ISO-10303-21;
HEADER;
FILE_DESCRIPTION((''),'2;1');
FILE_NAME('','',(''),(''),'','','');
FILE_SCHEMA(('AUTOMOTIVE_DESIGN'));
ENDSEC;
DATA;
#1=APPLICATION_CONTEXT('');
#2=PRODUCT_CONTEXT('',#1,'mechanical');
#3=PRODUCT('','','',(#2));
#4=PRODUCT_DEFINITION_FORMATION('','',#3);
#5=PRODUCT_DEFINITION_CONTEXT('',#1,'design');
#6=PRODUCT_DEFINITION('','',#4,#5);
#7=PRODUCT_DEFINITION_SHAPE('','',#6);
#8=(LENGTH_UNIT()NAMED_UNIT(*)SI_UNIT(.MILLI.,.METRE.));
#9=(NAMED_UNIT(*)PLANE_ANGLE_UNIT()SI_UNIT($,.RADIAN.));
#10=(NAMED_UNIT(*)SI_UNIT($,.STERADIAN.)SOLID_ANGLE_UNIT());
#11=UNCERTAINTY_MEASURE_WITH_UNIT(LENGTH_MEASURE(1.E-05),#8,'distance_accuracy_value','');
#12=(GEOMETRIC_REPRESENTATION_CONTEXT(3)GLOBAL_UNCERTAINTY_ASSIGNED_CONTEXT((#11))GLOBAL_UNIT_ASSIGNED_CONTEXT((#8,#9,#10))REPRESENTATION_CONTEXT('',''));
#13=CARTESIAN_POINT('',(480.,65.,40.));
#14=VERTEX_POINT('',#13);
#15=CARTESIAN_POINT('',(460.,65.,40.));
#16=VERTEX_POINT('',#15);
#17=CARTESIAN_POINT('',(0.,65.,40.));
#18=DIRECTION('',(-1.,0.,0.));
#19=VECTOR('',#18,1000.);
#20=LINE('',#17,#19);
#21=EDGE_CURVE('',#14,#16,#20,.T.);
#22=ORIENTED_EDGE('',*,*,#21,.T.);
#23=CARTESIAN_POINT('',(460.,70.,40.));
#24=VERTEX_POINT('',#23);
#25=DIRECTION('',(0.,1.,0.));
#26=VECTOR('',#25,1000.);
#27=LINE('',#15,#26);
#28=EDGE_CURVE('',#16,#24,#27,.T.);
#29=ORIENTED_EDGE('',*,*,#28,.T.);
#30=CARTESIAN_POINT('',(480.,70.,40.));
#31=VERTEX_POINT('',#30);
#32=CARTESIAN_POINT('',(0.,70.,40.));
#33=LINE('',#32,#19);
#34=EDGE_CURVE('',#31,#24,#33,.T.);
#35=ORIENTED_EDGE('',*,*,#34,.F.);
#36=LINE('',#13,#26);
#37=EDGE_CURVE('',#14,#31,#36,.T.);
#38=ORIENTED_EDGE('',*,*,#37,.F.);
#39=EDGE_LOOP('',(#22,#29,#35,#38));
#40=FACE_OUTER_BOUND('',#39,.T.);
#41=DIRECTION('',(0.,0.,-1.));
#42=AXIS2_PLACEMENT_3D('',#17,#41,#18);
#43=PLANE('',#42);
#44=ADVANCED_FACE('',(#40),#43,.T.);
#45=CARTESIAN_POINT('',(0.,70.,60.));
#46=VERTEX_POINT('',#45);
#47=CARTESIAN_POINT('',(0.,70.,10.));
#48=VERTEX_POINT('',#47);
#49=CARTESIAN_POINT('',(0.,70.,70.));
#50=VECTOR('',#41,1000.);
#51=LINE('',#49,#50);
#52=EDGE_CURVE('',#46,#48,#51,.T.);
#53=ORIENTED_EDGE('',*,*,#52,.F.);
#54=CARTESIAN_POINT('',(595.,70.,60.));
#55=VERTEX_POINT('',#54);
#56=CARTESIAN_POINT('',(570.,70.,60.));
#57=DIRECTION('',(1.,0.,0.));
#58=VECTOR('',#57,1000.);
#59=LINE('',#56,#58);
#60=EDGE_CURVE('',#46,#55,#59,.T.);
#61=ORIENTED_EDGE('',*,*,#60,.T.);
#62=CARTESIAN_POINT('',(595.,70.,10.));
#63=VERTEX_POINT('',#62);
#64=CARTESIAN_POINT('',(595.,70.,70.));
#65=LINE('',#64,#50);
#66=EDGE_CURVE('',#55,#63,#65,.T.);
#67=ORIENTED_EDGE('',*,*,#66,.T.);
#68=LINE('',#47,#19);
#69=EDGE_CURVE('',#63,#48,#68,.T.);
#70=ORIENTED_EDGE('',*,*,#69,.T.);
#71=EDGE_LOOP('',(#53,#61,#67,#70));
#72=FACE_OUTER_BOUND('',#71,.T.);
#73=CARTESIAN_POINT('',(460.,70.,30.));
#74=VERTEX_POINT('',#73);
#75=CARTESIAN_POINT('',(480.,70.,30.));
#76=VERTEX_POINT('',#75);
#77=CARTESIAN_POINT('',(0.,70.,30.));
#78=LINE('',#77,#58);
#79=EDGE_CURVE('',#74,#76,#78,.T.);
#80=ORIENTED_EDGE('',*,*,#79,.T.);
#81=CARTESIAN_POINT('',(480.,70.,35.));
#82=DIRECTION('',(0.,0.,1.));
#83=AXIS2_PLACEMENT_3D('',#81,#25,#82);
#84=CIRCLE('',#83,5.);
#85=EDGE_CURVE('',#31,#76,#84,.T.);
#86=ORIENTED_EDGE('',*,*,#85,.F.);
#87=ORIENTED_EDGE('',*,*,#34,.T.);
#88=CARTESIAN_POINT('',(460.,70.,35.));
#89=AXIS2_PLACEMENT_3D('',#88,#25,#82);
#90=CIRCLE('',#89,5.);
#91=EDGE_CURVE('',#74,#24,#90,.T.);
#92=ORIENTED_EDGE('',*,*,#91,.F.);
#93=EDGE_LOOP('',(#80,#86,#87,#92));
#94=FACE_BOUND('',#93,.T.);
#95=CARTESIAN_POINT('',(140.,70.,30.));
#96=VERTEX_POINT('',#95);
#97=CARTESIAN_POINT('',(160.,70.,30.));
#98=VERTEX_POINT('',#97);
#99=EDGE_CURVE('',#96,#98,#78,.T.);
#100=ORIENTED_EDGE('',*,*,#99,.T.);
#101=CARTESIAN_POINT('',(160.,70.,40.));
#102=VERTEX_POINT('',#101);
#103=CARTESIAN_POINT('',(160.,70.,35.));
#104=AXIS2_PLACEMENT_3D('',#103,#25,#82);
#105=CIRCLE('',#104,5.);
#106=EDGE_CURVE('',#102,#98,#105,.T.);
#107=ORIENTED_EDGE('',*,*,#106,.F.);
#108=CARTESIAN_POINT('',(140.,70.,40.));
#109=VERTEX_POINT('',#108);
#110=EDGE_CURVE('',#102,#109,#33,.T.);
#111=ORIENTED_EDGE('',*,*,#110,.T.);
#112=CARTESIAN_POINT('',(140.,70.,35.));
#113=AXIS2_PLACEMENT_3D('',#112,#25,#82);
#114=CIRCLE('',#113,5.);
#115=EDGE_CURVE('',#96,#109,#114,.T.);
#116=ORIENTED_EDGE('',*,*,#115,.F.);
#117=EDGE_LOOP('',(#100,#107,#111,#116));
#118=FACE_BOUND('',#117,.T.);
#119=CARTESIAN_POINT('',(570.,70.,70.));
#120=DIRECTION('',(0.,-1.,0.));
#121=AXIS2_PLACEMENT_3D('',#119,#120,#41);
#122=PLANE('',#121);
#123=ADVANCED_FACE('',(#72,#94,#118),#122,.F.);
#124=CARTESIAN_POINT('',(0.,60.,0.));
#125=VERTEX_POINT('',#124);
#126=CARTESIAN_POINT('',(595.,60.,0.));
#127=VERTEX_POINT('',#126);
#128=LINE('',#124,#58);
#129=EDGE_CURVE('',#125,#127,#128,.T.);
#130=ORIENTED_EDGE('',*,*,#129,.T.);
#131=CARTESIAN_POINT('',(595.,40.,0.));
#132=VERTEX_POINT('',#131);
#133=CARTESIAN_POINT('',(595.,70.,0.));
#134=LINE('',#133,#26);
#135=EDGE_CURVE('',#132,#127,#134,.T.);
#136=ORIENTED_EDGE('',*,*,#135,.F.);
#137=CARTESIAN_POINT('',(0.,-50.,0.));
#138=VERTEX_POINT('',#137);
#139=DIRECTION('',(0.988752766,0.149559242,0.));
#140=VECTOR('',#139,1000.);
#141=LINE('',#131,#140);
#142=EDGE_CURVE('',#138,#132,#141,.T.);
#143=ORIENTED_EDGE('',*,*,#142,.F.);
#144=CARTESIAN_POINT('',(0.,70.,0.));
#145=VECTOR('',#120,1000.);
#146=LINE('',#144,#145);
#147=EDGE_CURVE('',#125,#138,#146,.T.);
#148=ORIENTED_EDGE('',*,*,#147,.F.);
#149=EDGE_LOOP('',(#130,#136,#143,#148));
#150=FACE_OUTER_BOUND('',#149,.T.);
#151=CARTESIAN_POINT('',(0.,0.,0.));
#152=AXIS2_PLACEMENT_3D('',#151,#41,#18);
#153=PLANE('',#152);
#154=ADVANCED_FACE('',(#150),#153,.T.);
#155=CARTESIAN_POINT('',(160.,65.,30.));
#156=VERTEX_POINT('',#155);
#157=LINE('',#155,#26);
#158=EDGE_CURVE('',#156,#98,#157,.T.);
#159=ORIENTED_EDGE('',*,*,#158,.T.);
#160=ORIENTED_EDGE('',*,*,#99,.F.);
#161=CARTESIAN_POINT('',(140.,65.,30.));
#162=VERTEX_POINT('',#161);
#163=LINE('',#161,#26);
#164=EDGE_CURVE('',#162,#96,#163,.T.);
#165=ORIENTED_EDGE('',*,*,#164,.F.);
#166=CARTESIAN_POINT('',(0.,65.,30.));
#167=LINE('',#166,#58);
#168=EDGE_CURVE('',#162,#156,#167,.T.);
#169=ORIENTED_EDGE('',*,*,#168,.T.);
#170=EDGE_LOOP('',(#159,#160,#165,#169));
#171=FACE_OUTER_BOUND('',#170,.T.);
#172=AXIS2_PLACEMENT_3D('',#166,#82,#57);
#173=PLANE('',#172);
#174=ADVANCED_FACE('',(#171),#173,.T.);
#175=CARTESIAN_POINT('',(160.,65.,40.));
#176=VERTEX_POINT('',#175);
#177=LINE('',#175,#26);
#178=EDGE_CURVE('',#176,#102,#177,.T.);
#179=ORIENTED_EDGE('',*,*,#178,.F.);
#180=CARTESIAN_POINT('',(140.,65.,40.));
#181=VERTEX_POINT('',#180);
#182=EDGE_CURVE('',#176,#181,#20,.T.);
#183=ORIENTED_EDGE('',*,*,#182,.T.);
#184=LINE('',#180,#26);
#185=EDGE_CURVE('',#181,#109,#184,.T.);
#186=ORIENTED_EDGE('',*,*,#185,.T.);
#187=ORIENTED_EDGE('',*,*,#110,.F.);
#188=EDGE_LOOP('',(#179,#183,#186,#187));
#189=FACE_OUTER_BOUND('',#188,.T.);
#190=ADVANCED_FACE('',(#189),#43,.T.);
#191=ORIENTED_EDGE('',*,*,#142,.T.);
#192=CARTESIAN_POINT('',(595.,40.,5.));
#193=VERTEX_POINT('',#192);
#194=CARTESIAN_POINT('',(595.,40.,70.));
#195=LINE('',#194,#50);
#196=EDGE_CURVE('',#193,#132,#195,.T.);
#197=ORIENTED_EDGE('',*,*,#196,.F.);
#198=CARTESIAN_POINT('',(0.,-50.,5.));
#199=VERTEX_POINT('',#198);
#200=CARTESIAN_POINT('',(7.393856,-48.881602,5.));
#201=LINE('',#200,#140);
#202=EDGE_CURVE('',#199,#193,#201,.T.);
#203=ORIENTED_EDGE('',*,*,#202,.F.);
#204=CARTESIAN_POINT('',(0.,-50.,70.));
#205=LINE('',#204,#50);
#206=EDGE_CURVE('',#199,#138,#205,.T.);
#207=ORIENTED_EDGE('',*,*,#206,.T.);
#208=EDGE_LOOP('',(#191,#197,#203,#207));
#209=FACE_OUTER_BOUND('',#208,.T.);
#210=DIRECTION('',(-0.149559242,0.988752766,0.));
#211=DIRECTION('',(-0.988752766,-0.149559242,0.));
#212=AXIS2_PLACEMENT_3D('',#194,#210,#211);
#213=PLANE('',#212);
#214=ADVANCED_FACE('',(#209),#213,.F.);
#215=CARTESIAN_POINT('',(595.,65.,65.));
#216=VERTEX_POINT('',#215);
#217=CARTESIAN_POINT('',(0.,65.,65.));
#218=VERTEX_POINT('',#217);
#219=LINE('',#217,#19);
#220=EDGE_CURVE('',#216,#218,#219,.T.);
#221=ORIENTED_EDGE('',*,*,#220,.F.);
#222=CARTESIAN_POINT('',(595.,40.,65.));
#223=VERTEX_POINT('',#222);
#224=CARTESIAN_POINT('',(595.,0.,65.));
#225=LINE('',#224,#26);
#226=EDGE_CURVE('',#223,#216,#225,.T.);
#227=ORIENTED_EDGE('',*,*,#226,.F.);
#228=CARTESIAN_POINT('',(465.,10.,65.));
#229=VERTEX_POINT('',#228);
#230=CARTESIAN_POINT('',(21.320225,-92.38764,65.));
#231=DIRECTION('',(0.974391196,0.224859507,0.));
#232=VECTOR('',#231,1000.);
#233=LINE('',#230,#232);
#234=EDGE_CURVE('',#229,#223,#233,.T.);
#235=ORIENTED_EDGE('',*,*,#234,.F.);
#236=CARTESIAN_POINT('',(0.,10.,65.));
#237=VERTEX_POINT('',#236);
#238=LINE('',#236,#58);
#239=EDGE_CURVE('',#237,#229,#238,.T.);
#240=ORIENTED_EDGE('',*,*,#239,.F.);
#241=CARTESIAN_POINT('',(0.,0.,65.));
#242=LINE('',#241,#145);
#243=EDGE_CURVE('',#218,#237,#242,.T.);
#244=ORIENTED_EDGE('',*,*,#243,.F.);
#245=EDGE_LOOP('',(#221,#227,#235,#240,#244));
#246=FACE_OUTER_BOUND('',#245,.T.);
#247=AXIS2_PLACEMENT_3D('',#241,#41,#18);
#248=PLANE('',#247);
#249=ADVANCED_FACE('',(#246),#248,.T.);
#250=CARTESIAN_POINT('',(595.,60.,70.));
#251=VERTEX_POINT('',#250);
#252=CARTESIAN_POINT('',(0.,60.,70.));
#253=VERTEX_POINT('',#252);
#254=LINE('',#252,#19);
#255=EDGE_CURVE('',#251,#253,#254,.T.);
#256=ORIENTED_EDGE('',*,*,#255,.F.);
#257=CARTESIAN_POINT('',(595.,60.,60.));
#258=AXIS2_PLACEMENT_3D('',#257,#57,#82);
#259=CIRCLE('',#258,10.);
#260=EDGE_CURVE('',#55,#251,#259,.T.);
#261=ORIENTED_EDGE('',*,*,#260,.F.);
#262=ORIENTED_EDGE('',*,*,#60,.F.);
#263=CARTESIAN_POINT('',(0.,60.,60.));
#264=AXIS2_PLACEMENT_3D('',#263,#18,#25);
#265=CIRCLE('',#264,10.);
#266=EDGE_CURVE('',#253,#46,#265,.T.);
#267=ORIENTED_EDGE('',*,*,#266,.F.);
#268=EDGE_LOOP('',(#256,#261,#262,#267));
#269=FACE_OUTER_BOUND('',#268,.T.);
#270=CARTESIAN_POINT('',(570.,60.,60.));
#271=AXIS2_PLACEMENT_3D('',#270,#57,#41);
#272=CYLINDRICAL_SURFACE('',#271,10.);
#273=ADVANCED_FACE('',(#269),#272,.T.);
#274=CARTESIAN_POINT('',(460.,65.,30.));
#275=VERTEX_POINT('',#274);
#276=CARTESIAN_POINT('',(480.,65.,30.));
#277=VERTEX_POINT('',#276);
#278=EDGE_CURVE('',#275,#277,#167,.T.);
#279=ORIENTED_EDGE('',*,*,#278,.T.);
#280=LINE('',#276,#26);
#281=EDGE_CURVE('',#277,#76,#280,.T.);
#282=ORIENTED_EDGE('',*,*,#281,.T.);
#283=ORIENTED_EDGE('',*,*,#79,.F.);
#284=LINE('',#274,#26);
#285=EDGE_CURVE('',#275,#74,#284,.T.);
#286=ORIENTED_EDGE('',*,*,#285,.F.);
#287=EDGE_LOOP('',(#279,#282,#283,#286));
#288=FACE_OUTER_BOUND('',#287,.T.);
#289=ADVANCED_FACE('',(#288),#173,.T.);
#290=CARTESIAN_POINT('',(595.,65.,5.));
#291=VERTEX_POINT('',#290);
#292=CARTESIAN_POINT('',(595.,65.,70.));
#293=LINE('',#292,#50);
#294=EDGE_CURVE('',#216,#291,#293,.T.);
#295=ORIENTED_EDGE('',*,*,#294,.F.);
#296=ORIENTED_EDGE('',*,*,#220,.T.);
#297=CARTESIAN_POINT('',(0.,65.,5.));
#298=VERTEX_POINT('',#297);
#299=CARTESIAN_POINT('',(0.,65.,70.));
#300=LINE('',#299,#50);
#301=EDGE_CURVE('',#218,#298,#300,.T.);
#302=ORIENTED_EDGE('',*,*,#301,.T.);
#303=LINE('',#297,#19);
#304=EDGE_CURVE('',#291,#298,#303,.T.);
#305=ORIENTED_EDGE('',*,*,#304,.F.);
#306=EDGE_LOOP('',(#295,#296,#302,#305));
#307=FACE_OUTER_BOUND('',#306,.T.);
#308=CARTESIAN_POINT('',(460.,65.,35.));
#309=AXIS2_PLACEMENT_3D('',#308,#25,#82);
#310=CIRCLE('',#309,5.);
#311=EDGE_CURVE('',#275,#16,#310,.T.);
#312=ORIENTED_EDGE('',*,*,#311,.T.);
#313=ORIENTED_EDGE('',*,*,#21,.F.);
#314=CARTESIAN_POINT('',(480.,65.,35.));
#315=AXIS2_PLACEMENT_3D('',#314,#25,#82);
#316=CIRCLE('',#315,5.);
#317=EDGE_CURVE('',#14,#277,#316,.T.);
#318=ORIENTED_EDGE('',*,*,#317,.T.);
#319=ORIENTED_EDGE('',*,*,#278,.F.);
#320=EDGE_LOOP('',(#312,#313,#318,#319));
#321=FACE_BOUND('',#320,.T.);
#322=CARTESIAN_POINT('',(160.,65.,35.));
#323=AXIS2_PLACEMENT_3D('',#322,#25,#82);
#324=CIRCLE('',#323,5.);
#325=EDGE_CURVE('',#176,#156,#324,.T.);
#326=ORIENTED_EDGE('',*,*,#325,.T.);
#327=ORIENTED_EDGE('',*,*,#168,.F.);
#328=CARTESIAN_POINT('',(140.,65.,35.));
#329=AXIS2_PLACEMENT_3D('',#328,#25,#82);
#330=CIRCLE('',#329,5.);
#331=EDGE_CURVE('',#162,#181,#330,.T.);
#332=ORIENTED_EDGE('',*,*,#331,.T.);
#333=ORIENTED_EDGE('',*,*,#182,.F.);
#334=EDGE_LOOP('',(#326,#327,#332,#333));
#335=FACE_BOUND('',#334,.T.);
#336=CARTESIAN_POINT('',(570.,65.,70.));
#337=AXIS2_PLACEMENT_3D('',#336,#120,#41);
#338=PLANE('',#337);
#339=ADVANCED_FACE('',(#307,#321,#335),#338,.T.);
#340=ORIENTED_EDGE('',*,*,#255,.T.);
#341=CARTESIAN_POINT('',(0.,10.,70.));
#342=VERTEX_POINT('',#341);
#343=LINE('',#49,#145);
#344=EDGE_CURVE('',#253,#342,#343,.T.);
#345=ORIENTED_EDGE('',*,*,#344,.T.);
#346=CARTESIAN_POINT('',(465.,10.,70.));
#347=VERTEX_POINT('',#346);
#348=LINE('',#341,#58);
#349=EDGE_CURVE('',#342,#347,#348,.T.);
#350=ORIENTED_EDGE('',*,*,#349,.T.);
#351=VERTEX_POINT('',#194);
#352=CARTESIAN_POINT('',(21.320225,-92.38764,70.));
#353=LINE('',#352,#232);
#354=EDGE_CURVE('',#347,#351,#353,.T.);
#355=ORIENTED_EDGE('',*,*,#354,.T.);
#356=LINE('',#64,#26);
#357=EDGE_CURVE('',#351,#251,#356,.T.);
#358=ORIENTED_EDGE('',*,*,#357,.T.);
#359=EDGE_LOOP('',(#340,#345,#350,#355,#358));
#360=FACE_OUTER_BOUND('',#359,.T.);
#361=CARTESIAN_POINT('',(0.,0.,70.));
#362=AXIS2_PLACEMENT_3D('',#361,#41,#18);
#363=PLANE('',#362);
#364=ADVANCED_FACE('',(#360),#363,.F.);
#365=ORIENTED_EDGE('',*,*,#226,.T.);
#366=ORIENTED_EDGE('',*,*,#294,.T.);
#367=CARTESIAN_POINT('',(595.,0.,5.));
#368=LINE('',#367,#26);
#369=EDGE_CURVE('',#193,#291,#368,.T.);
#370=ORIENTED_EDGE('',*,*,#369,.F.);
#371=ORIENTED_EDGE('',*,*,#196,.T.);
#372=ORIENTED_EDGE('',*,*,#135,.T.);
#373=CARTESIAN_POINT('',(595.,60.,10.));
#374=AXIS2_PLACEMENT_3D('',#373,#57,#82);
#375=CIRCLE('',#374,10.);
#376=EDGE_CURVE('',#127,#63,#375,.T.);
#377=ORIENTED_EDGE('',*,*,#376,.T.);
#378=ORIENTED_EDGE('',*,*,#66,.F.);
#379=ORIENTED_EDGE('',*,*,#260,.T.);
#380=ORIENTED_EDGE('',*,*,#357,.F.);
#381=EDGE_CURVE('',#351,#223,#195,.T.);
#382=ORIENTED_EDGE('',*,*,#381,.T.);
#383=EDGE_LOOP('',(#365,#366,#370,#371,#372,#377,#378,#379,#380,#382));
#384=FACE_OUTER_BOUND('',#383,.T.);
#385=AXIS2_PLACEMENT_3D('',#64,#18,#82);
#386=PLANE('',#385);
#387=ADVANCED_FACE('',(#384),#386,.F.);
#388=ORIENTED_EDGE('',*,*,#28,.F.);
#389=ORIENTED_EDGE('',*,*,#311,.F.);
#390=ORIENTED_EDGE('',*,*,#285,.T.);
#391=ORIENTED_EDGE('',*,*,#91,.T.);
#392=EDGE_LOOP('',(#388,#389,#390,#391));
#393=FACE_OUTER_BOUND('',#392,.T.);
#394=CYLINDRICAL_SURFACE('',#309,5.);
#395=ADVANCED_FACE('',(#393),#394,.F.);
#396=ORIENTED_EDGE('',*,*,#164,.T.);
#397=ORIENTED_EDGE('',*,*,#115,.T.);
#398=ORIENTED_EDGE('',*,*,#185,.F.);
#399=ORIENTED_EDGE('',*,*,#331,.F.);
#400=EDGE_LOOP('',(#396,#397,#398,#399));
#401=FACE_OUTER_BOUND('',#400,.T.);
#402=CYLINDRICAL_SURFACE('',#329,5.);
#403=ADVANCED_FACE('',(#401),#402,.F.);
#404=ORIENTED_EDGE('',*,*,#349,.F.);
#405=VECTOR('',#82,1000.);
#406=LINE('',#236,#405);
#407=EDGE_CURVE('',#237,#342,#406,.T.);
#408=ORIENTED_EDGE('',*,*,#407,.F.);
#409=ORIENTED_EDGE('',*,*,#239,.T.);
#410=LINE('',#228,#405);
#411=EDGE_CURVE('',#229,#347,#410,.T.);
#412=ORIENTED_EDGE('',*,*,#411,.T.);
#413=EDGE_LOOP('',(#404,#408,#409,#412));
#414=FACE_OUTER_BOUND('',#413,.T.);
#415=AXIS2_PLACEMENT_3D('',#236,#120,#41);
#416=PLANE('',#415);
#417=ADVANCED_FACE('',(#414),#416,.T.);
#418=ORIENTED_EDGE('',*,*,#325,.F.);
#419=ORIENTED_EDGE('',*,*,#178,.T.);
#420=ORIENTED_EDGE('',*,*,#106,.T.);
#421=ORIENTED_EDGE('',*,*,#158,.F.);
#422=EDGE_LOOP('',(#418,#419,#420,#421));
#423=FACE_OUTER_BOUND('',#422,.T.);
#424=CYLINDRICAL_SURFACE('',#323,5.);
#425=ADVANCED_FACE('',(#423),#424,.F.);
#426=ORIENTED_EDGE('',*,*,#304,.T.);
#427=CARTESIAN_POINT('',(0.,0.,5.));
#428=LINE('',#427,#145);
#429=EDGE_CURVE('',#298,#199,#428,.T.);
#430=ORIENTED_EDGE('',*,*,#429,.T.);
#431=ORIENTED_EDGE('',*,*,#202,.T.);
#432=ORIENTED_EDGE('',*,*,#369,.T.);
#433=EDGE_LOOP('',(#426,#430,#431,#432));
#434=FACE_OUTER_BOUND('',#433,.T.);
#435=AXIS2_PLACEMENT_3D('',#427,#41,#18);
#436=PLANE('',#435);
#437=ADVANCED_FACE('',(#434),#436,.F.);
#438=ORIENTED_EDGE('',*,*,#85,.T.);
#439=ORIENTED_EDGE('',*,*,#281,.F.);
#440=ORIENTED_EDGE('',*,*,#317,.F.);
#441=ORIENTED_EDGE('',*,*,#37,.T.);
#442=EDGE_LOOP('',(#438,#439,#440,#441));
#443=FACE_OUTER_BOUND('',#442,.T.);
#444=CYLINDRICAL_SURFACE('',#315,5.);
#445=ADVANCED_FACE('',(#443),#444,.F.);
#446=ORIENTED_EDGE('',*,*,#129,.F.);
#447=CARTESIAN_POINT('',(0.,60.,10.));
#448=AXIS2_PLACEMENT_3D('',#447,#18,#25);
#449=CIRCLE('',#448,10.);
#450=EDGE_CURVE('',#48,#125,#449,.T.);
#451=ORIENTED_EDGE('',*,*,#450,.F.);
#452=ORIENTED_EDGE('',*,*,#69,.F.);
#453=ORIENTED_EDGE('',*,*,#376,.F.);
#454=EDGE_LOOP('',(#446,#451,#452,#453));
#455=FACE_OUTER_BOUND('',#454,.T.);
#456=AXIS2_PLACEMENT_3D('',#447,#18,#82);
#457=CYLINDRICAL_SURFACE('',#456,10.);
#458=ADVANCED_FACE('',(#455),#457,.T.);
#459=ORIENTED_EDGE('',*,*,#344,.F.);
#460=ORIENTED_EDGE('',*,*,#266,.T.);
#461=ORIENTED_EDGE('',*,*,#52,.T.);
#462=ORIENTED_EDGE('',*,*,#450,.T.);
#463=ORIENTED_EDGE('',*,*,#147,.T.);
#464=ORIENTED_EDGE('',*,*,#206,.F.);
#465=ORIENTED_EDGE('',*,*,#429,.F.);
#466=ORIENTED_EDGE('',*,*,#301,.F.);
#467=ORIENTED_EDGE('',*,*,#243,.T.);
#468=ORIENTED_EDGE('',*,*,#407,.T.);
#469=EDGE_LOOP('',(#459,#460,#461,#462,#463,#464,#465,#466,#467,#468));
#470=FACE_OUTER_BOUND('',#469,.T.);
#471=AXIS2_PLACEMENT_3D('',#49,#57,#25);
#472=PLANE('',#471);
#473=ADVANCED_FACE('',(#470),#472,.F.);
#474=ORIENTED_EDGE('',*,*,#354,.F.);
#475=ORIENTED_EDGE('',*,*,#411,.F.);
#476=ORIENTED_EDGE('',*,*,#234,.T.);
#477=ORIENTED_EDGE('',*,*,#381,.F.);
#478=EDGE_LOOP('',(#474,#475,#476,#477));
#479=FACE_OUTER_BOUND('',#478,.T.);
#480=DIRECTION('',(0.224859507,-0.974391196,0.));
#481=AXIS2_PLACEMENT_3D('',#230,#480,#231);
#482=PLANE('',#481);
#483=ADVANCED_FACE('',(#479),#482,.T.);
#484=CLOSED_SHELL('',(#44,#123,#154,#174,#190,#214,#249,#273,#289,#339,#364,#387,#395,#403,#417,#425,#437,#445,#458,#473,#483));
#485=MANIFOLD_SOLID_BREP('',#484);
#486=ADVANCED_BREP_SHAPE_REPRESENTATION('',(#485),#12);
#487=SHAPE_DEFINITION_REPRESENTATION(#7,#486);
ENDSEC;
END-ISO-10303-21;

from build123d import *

# Parameters (mm, degrees)
EXTRUDE_1_DEPTH     = 70
SHELL_1_T           = -5
EXTRUDE_2_DEPTH     = 5
CUT_EXTRUDE_1_DEPTH = 5
FILLET_1_R          = 10
FILLET_2_R          = 10
CUT_EXTRUDE_2_DEPTH = 5


with BuildPart() as part:
    # 草图1 → 凸台-拉伸1 (new body)
    with BuildSketch(Plane.XY):
        Polygon((0, 70), (0, -50), (595, 40), (595, 70), (570, 70), align=None)
    extrude(amount=EXTRUDE_1_DEPTH)

    # 抽壳1
    shell_1_openings = [part.faces().sort_by_distance(p)[0] for p in [
        (0, 10, 35),
        (595, 55, 35),
        (297.5, -5, 35),
    ]]
    offset(amount=SHELL_1_T, openings=shell_1_openings, kind=Kind.INTERSECTION)

    # 草图2 → 凸台-拉伸2 (add)
    with BuildSketch(Plane.XY.offset(70)):
        Polygon((465, 10), (595, 40), (396.666666667, 10), align=None)
    extrude(amount=-EXTRUDE_2_DEPTH)

    # 草图3 → 切除-拉伸1 (cut)
    with BuildSketch(Plane.XY.offset(70)):
        Polygon((0, -50), (396.666666667, 10), (0, 10), align=None)
    extrude(amount=-CUT_EXTRUDE_1_DEPTH, mode=Mode.SUBTRACT)

    # 圆角1
    fillet_1_edges = [part.edges().sort_by_distance(p)[0] for p in [
        (297.5, 70, 70),
    ]]
    fillet(fillet_1_edges, radius=FILLET_1_R)

    # 圆角2
    fillet_2_edges = [part.edges().sort_by_distance(p)[0] for p in [
        (297.5, 70, 0),
    ]]
    fillet(fillet_2_edges, radius=FILLET_2_R)

    # 草图4 → 切除-拉伸2 (cut)
    with BuildSketch(Plane(origin=(0, 70, 0), x_dir=(1, 0, 0), z_dir=(0, 1, 0))):
        with BuildLine():
            Line((160, -40), (140, -40))
            ThreePointArc((140, -40), (135, -35), (140, -30))
            Line((140, -30), (160, -30))
            ThreePointArc((160, -30), (165, -35), (160, -40))
        make_face()
        with BuildLine():
            Line((460, -30), (480, -30))
            ThreePointArc((480, -30), (485, -35), (480, -40))
            Line((480, -40), (460, -40))
            ThreePointArc((460, -40), (455, -35), (460, -30))
        make_face()
    extrude(amount=-CUT_EXTRUDE_2_DEPTH, mode=Mode.SUBTRACT)


solid = part.part
